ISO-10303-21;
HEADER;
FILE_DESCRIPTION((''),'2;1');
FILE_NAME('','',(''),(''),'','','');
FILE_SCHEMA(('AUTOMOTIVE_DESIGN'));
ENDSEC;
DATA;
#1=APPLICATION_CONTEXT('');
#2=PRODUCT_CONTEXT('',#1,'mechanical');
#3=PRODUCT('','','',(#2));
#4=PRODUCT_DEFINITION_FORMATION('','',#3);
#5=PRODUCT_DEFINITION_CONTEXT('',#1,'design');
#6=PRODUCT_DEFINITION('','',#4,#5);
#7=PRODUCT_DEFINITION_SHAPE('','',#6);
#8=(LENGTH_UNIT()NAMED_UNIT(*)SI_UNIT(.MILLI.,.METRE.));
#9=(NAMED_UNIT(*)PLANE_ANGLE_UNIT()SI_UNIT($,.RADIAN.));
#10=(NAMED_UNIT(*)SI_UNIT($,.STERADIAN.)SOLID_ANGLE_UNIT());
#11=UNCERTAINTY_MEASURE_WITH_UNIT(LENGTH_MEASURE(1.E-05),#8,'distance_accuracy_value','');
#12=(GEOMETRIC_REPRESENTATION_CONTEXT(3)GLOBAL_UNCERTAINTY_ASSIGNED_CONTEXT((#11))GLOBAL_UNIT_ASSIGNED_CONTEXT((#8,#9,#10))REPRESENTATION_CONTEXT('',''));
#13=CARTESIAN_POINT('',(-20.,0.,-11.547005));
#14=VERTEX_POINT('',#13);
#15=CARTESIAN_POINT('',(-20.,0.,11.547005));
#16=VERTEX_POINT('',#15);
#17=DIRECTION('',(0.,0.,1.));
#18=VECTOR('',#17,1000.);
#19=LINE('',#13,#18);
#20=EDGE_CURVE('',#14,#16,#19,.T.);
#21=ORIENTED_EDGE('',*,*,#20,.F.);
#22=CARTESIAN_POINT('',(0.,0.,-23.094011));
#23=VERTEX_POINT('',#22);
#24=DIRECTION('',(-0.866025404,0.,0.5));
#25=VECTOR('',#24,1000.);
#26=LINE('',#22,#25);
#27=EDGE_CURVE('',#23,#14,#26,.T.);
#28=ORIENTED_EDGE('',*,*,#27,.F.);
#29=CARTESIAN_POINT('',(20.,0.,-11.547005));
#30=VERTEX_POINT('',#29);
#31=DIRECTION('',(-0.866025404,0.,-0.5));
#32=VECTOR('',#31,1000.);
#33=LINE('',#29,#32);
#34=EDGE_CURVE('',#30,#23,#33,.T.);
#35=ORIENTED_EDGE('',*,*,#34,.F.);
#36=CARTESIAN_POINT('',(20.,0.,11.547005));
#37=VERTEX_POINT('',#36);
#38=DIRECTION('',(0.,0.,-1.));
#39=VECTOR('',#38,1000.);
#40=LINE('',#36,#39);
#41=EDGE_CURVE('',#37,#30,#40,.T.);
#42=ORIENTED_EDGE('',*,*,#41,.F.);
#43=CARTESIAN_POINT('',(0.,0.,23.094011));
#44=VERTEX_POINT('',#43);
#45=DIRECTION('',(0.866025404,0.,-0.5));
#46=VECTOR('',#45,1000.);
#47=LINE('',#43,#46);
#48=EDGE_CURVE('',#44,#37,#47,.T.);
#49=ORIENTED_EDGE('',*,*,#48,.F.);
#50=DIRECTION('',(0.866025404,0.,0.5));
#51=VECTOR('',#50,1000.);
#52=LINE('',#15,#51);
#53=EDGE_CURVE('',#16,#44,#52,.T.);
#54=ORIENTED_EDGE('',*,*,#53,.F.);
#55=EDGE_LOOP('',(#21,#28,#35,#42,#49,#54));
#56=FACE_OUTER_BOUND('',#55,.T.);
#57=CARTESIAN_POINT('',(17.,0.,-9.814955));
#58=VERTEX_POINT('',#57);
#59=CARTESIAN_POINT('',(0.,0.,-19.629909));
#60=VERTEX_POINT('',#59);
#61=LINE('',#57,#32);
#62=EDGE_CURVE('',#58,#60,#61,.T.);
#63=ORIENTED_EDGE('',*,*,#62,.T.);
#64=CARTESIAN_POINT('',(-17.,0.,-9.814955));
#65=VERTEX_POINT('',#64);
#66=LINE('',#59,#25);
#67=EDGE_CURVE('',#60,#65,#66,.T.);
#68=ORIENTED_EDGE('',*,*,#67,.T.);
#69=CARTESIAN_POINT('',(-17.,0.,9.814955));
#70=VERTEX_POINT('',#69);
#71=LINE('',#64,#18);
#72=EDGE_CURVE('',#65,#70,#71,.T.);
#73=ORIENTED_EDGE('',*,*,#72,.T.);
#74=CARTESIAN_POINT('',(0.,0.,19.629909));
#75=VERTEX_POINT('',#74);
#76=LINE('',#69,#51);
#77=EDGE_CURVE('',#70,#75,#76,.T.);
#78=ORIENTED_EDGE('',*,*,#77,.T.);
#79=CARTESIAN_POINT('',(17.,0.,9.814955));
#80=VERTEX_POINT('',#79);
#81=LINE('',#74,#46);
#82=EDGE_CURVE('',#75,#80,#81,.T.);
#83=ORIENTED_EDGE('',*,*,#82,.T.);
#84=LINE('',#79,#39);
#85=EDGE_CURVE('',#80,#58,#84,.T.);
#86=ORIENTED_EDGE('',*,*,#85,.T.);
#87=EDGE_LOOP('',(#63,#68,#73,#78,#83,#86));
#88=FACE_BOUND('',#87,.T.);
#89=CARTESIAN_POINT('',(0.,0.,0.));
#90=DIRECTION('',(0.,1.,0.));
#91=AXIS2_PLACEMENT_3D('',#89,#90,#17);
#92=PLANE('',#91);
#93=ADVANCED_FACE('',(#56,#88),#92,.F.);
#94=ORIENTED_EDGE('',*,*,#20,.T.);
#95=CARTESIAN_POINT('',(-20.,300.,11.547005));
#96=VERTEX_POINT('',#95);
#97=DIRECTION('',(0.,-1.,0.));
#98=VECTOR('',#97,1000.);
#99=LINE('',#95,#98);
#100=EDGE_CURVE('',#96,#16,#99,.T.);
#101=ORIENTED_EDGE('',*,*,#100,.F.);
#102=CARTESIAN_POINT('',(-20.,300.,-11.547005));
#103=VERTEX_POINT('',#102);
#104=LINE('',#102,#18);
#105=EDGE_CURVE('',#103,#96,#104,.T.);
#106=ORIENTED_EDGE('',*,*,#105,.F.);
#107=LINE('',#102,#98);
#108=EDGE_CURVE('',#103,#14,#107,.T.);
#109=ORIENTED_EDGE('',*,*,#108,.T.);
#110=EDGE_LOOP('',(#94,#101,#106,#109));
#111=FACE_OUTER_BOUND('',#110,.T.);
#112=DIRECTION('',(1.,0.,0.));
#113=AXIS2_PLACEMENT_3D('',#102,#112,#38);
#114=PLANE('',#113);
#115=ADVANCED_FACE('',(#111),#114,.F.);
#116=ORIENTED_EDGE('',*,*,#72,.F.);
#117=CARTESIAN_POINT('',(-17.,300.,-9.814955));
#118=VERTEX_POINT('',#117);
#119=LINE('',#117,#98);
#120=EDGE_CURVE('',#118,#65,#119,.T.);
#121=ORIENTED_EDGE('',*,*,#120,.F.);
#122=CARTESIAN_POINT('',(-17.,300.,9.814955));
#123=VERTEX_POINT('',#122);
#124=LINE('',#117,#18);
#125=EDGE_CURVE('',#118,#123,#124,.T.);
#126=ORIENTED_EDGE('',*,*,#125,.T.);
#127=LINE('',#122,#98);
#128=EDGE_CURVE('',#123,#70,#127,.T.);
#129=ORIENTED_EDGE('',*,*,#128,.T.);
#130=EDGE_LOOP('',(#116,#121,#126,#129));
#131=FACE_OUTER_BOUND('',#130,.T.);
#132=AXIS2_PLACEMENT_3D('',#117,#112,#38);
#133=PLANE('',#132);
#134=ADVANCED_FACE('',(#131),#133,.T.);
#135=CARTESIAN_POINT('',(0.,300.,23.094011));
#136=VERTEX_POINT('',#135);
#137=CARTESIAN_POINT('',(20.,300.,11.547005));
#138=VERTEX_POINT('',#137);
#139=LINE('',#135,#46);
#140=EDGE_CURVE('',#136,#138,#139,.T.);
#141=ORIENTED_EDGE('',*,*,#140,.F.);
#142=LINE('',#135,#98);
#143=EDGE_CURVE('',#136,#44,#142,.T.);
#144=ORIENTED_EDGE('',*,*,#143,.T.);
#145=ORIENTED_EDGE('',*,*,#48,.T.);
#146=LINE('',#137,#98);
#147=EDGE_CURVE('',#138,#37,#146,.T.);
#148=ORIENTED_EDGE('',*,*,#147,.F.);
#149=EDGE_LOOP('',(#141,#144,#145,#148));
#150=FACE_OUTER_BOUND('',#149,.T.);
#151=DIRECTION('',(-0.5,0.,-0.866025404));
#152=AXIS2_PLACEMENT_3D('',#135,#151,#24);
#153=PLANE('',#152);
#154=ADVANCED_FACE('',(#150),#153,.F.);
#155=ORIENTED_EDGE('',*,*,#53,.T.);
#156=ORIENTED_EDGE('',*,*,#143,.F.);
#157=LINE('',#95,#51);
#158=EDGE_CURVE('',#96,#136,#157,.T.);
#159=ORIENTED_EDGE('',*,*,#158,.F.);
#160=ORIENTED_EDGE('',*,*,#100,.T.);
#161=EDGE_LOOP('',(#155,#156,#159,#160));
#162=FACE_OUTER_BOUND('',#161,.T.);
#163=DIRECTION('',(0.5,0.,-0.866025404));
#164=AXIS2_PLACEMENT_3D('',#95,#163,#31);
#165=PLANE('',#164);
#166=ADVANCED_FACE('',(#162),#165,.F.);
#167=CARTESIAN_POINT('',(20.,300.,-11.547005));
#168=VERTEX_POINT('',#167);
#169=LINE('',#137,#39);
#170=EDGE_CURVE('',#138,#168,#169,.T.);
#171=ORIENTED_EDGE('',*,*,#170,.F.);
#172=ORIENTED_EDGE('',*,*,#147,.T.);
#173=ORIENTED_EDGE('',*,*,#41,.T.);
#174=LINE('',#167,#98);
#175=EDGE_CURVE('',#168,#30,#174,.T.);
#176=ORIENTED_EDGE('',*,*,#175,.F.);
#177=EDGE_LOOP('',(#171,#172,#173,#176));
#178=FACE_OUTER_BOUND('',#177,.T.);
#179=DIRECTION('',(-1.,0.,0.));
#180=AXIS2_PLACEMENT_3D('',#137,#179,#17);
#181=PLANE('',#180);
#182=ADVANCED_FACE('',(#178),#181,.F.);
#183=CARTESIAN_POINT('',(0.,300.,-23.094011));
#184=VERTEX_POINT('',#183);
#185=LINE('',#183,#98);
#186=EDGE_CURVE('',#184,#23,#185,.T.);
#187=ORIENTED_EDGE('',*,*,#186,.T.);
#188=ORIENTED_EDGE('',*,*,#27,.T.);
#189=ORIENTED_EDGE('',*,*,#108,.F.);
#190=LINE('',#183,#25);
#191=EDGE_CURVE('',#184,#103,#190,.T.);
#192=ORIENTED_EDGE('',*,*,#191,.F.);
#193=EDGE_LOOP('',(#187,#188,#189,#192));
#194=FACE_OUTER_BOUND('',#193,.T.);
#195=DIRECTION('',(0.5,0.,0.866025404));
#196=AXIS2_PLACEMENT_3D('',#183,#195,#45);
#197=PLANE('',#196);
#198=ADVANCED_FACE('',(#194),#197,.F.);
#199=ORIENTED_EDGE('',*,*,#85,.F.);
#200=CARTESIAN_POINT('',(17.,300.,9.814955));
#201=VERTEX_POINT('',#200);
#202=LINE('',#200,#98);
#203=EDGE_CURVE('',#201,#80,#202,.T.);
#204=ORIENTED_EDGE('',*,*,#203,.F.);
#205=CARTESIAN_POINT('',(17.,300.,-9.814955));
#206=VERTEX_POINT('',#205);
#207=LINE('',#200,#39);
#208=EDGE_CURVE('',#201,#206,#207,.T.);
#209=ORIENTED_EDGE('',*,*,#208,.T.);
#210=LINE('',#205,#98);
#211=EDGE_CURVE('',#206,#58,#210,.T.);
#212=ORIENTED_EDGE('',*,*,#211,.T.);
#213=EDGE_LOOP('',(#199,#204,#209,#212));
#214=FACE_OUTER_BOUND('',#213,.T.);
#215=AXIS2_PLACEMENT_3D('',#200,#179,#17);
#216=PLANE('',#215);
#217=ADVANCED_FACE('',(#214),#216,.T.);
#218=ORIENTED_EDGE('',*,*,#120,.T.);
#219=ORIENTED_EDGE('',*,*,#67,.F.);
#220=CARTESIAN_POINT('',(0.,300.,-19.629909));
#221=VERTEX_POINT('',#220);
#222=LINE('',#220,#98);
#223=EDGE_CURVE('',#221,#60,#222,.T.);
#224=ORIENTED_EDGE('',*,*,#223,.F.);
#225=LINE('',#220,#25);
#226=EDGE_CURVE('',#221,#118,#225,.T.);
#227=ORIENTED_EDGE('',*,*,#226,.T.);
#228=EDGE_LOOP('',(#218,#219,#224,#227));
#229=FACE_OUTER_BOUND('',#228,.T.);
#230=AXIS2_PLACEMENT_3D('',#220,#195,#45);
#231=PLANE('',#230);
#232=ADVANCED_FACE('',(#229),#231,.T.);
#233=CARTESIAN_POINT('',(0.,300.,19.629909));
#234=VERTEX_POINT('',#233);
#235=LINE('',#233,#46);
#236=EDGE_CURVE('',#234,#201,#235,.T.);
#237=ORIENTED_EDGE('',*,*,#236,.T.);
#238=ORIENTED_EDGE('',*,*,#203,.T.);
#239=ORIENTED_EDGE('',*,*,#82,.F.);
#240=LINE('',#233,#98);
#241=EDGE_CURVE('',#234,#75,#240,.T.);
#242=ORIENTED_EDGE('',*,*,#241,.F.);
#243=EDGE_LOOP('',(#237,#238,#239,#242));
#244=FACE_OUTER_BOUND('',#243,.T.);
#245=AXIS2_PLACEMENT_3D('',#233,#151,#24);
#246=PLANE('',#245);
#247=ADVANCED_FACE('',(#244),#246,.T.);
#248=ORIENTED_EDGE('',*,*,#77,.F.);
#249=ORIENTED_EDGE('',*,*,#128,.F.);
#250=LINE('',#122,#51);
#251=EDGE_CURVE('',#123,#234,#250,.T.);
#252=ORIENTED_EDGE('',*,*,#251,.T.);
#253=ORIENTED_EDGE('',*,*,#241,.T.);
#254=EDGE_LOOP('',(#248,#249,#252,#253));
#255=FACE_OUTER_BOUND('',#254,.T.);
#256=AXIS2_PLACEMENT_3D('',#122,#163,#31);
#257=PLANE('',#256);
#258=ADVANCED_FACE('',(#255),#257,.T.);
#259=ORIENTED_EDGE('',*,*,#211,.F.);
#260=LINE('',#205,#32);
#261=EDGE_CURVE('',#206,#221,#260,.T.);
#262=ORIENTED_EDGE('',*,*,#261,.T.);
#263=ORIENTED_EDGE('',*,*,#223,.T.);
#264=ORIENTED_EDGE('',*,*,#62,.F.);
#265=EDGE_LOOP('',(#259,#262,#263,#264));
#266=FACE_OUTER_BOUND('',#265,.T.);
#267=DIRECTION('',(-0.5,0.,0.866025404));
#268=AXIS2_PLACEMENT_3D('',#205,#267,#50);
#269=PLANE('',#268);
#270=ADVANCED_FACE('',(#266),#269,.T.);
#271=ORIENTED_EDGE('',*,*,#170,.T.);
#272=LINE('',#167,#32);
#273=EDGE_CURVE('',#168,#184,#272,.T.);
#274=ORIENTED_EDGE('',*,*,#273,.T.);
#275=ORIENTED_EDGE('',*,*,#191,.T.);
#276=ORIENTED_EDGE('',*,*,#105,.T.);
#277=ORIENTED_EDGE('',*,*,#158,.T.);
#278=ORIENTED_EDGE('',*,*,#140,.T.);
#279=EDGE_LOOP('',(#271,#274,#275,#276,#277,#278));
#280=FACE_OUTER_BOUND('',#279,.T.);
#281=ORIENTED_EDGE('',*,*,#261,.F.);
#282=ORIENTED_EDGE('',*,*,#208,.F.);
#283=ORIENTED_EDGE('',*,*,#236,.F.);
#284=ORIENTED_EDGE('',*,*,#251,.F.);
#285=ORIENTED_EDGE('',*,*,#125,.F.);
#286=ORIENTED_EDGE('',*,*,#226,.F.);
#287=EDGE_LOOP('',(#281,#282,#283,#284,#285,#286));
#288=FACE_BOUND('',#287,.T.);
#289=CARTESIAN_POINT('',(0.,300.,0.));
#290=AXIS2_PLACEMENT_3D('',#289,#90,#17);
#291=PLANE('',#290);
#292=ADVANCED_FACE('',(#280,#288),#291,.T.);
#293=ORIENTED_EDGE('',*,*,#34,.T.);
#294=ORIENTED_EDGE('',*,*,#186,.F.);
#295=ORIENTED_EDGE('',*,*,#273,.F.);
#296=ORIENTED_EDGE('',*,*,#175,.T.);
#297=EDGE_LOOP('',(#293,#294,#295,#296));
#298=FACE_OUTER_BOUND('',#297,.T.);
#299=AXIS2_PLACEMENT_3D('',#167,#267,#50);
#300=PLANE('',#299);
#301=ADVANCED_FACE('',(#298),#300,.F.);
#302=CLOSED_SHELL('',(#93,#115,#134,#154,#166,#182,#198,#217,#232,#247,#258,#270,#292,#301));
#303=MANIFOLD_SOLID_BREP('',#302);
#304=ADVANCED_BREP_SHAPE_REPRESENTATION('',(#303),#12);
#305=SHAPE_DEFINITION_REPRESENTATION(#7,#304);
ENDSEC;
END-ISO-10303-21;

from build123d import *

# Parameters (mm, degrees)
BOSS_EXTRUDE1_DEPTH = 300


with BuildPart() as part:
    # Sketch1 → Boss-Extrude1 (new body)
    with BuildSketch(Plane(origin=(0, 0, 0), x_dir=(1, 0, 0), z_dir=(0, 1, 0))):
        Polygon((0, 23.094010768), (-20, 11.547005384), (-20, -11.547005384), (0, -23.094010768), (20, -11.547005384), (20, 11.547005384), align=None)
        Polygon((-17, 9.814954576), (-17, -9.814954576), (0, -19.629909152), (17, -9.814954576), (17, 9.814954576), (0, 19.629909152), align=None, mode=Mode.SUBTRACT)
    extrude(amount=BOSS_EXTRUDE1_DEPTH)


solid = part.part
